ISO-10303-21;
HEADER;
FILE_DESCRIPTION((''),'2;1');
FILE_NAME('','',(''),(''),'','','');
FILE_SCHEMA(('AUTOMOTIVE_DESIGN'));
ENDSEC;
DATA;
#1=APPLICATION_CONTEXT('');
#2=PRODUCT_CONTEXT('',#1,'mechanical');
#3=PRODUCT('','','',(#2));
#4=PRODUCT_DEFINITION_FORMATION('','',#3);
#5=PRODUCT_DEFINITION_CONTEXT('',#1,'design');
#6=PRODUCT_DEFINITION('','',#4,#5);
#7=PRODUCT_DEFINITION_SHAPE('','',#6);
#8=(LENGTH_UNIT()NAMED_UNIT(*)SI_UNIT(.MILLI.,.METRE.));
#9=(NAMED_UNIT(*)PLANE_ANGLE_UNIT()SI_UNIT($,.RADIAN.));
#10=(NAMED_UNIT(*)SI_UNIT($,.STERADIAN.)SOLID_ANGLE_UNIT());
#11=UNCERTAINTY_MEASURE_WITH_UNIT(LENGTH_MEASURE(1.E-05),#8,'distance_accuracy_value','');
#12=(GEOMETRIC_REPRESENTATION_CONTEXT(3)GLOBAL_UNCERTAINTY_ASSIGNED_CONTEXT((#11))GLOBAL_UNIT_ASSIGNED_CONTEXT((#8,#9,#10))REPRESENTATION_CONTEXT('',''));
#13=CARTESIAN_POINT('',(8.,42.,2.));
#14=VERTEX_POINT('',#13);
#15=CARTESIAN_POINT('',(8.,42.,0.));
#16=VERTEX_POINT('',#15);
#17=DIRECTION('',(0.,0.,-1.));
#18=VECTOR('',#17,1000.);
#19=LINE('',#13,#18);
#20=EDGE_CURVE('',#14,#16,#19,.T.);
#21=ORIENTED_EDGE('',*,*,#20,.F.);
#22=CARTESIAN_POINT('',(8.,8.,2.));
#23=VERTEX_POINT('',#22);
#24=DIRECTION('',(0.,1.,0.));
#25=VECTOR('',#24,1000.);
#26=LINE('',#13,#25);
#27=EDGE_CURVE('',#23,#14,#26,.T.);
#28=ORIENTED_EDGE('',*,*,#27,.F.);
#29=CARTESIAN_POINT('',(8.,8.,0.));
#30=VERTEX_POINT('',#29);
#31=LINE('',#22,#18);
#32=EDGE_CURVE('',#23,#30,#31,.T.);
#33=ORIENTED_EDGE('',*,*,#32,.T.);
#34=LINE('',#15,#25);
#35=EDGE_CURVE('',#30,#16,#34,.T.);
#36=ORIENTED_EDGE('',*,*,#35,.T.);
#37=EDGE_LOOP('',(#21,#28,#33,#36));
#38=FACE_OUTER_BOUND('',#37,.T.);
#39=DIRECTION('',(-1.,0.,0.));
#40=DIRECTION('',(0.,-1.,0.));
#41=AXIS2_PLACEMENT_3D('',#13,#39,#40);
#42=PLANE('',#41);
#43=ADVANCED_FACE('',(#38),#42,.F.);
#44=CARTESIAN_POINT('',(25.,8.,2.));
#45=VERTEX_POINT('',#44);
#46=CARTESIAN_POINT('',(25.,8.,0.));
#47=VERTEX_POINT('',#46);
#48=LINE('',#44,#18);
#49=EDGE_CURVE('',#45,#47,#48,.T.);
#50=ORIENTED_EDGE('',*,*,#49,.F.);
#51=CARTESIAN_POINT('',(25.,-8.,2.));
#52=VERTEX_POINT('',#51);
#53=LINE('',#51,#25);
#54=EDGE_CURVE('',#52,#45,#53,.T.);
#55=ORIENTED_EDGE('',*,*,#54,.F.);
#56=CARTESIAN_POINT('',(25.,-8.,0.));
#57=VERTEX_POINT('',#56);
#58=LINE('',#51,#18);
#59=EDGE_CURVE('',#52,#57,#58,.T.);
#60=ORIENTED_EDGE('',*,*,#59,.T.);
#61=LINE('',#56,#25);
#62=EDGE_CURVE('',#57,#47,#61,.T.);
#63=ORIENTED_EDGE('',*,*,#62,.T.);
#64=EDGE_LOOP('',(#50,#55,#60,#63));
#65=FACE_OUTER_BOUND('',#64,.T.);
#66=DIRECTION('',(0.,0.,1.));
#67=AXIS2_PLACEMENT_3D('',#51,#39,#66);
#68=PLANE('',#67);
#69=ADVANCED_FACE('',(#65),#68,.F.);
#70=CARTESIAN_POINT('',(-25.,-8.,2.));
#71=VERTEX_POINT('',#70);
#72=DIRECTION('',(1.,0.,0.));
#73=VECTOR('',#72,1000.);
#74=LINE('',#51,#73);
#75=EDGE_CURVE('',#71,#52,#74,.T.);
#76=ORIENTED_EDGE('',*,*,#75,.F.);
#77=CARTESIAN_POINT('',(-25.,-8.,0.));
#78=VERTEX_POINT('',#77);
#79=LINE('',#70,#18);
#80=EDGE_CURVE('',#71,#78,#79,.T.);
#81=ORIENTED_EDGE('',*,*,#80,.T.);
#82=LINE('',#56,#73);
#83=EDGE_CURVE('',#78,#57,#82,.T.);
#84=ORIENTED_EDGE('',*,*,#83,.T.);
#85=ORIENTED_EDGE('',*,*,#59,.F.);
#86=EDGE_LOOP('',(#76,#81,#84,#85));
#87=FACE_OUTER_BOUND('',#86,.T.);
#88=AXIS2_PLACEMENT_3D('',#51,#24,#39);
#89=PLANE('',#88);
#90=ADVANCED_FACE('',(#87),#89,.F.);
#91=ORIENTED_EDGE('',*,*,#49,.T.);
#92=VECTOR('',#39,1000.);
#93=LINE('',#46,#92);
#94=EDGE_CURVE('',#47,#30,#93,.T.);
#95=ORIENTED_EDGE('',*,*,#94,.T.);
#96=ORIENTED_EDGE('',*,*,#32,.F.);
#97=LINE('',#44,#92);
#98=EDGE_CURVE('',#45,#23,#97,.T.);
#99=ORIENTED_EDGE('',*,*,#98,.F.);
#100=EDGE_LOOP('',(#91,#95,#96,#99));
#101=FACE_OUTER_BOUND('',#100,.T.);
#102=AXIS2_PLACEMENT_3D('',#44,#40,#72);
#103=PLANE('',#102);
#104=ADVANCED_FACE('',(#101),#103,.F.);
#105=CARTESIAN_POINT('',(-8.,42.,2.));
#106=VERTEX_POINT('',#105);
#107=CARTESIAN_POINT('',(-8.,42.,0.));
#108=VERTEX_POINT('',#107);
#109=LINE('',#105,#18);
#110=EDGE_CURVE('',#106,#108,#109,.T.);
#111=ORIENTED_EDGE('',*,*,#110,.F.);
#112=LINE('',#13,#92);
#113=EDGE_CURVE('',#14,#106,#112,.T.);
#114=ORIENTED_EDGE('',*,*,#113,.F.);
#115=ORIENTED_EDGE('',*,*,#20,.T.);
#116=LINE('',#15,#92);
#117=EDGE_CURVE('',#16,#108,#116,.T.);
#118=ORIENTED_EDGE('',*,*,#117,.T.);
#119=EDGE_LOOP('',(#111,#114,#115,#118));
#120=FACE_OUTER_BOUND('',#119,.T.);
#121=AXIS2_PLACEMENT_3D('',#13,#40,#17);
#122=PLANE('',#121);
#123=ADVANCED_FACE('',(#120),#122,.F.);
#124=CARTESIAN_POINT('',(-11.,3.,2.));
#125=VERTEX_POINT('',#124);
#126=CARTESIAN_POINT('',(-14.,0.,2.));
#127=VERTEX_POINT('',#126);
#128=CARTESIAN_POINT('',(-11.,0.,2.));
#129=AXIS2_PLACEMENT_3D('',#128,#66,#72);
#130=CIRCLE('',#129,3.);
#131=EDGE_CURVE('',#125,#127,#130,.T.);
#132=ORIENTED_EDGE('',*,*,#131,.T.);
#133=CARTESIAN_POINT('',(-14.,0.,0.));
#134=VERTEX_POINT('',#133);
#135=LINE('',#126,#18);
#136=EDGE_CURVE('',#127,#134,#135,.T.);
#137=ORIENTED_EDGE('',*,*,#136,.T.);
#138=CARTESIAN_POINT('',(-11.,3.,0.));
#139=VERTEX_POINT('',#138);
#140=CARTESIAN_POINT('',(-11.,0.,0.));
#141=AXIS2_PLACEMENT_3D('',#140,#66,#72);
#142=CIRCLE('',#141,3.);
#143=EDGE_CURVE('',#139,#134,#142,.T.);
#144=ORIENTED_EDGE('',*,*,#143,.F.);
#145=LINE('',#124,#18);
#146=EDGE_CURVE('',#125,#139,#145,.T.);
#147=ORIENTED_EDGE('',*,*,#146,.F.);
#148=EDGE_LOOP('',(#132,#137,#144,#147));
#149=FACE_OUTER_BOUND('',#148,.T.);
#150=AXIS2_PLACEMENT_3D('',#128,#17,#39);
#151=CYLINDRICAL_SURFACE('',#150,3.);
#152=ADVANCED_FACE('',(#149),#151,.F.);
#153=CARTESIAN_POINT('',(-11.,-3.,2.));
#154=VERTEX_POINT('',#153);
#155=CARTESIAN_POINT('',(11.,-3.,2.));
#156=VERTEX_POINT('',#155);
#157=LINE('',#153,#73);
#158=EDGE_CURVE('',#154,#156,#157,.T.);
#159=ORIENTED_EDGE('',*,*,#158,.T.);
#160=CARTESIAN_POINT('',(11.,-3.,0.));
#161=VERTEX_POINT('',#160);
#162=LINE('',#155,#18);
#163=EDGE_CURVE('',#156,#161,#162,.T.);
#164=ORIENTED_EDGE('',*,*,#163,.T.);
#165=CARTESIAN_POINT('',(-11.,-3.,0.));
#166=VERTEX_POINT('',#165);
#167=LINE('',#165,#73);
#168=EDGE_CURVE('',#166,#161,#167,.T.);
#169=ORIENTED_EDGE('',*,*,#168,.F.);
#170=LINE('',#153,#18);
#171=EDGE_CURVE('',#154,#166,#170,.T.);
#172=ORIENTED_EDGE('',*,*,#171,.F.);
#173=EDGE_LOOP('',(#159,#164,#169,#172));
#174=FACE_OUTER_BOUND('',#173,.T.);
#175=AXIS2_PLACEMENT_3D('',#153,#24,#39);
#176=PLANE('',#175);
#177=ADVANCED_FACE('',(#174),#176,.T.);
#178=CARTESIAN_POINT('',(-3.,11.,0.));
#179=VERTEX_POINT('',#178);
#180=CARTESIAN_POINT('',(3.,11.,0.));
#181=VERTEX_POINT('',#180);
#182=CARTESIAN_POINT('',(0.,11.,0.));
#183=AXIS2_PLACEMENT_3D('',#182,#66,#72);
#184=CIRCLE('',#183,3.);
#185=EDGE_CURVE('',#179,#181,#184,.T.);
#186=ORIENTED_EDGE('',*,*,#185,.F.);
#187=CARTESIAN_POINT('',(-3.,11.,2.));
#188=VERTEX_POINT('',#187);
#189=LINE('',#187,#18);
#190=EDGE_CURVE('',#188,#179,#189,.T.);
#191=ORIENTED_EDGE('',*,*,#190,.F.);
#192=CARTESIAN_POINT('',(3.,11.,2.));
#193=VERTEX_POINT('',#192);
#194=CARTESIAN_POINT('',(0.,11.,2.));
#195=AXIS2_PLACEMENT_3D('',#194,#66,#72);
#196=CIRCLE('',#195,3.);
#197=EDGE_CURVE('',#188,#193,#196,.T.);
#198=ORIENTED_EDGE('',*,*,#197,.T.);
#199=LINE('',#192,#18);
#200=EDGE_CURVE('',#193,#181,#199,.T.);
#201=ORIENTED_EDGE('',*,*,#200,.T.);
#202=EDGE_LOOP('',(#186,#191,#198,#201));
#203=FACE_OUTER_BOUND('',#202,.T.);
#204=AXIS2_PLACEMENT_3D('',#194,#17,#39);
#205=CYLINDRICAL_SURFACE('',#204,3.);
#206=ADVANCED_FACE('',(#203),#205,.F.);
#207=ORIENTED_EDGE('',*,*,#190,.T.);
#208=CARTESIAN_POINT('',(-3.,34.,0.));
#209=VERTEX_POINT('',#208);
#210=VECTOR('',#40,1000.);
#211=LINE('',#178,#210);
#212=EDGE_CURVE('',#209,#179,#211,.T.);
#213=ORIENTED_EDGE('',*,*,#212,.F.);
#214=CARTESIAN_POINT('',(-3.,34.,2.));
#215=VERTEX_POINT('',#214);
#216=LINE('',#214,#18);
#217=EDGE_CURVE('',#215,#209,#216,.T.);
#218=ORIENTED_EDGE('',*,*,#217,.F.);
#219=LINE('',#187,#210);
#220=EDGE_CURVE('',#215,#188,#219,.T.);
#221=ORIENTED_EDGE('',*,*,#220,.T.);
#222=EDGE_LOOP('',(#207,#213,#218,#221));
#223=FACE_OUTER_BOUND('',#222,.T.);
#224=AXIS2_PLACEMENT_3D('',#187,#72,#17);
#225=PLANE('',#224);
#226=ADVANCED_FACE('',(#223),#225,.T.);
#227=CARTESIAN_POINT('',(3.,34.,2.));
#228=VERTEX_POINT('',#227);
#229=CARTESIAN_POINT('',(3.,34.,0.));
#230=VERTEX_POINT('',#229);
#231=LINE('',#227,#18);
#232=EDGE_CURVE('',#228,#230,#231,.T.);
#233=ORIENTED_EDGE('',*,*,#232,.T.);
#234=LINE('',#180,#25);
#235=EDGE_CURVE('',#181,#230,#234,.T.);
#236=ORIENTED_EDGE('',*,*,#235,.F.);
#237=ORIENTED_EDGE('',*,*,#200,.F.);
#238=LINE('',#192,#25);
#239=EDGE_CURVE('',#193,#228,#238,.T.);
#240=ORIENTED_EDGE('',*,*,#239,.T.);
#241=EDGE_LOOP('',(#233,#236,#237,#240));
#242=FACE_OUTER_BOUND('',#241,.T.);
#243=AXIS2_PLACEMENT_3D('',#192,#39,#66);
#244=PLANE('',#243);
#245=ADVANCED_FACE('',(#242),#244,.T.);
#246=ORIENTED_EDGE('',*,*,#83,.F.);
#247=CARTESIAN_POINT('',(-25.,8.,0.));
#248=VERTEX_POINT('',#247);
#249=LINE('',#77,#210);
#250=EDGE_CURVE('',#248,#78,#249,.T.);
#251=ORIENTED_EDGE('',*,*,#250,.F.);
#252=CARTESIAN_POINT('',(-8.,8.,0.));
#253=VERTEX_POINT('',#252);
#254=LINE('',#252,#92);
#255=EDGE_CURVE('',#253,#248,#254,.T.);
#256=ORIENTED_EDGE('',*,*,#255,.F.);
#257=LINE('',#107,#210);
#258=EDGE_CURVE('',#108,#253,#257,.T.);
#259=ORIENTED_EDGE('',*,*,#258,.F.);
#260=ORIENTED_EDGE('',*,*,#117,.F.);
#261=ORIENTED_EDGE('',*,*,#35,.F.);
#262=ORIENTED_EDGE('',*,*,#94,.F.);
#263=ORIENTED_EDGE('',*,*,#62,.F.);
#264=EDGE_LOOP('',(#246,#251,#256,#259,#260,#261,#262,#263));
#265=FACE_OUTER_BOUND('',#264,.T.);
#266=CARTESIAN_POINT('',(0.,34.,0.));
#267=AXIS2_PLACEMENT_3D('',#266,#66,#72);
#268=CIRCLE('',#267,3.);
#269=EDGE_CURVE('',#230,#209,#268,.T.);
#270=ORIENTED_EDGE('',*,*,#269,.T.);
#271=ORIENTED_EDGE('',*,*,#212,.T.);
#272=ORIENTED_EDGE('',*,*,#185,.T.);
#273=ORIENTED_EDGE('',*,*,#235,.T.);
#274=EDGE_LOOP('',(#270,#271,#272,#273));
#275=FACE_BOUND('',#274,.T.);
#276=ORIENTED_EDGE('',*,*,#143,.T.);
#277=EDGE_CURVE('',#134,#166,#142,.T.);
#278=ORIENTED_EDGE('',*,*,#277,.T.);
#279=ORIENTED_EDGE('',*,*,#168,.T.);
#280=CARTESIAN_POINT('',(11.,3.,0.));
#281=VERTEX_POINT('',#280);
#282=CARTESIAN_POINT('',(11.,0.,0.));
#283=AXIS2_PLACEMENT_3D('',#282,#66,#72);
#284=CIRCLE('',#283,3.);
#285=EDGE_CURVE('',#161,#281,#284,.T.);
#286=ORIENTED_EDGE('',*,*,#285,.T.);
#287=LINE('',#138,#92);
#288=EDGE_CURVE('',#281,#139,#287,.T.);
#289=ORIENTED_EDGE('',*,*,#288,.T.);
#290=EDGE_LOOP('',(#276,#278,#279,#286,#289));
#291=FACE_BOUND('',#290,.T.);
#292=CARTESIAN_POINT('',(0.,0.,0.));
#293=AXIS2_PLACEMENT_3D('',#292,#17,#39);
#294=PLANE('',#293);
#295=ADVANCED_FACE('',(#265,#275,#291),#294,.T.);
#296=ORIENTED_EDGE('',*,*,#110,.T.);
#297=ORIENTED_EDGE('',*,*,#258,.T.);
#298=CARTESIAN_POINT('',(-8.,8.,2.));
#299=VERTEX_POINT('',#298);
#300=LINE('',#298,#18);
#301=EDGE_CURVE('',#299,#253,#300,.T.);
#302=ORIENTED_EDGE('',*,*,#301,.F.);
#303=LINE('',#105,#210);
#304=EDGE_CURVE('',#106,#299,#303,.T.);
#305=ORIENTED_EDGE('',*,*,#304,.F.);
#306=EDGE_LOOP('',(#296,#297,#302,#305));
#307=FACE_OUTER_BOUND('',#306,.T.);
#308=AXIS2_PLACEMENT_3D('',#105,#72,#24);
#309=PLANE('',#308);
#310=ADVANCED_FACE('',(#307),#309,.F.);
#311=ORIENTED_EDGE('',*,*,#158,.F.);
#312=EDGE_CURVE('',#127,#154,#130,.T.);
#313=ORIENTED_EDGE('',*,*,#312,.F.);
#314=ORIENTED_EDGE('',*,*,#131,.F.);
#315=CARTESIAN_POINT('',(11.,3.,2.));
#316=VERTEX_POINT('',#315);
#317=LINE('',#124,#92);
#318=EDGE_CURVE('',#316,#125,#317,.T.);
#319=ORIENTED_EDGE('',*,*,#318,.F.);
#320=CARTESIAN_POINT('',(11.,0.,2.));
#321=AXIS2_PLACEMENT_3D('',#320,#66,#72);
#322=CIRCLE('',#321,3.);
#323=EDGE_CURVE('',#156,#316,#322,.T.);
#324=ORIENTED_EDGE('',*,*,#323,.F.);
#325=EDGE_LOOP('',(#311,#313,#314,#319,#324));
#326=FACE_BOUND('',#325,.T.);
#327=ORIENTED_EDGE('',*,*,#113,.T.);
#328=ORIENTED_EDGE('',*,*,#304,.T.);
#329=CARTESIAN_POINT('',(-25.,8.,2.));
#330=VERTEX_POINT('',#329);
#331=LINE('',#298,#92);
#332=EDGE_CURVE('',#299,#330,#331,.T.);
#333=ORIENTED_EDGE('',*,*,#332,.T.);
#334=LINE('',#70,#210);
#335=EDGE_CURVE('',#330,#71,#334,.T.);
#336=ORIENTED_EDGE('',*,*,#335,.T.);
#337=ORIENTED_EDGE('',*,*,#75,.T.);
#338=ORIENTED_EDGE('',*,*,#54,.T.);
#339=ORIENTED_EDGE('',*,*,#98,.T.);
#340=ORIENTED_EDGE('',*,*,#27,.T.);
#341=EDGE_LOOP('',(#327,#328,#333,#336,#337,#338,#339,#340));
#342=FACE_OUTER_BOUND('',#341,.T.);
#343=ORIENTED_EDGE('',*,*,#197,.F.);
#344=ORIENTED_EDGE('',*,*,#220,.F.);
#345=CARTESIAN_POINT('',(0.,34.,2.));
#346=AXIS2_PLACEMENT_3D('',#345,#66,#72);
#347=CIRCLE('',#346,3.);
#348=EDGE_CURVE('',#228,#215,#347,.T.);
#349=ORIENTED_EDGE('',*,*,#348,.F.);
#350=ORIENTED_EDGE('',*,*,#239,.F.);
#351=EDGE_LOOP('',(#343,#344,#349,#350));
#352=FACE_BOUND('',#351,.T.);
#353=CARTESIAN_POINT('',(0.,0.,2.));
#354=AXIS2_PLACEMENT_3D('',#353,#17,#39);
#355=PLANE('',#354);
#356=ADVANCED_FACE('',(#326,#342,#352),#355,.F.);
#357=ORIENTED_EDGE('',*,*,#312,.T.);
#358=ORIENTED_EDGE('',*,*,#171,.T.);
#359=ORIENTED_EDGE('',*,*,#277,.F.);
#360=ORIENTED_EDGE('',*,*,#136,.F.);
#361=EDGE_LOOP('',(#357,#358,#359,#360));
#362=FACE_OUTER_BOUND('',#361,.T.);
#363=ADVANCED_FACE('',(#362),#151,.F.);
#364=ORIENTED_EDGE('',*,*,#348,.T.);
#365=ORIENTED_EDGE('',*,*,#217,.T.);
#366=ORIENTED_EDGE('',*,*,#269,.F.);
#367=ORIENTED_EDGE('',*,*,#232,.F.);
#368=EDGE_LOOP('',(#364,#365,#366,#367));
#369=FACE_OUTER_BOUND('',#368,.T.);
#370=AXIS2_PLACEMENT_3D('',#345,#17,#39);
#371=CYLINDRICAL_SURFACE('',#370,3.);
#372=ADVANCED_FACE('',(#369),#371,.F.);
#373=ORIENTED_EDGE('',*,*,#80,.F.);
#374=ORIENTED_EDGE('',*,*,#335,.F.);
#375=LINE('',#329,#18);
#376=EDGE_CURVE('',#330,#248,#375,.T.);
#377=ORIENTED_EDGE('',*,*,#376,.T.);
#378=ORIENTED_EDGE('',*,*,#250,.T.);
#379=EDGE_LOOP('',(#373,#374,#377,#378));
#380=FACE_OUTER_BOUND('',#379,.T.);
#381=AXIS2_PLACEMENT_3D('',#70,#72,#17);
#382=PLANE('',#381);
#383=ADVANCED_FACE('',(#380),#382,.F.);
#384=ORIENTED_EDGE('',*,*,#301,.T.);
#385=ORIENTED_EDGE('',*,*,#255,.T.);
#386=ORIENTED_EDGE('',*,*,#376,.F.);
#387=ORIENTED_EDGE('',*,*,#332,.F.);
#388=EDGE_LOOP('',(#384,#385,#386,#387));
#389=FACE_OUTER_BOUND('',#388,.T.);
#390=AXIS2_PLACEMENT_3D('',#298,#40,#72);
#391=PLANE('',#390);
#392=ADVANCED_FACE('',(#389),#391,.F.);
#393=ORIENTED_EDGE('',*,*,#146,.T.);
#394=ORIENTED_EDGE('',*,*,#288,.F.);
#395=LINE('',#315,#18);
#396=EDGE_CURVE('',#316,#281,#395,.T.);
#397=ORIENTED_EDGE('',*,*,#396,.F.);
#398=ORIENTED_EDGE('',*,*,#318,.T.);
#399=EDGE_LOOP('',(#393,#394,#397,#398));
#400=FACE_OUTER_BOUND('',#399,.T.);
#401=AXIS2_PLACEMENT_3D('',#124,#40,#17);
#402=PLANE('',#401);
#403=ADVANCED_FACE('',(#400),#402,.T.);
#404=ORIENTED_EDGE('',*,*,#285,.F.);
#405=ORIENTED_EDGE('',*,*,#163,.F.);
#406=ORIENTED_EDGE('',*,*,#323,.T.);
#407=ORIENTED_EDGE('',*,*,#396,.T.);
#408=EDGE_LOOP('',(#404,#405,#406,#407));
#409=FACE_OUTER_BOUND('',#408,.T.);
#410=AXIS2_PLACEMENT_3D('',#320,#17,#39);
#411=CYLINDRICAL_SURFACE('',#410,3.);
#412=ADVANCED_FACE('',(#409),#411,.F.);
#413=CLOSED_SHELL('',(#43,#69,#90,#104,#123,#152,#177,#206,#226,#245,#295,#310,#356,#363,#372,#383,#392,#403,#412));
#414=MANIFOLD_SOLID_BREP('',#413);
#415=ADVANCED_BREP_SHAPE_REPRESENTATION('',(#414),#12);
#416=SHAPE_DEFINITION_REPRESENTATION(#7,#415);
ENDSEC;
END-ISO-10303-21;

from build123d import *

# Parameters (mm, degrees)
EXTRUDE_2_DEPTH = 2


with BuildPart() as part:
    # 草图1 → 凸台-拉伸2 (new body)
    with BuildSketch(Plane.XY):
        Polygon((25, -8), (-25, -8), (-25, 8), (-8, 8), (-8, 42), (8, 42), (8, 8), (25, 8), align=None)
        with BuildLine():
            Line((-3, 11), (-3, 34))
            ThreePointArc((-3, 34), (0, 37), (3, 34))
            Line((3, 34), (3, 11))
            ThreePointArc((3, 11), (0, 8), (-3, 11))
        make_face(mode=Mode.SUBTRACT)
        with BuildLine():
            Line((-11, 3), (11, 3))
            ThreePointArc((11, 3), (14, 0), (11, -3))
            Line((11, -3), (-11, -3))
            ThreePointArc((-11, -3), (-14, 0), (-11, 3))
        make_face(mode=Mode.SUBTRACT)
    extrude(amount=EXTRUDE_2_DEPTH)


solid = part.part
